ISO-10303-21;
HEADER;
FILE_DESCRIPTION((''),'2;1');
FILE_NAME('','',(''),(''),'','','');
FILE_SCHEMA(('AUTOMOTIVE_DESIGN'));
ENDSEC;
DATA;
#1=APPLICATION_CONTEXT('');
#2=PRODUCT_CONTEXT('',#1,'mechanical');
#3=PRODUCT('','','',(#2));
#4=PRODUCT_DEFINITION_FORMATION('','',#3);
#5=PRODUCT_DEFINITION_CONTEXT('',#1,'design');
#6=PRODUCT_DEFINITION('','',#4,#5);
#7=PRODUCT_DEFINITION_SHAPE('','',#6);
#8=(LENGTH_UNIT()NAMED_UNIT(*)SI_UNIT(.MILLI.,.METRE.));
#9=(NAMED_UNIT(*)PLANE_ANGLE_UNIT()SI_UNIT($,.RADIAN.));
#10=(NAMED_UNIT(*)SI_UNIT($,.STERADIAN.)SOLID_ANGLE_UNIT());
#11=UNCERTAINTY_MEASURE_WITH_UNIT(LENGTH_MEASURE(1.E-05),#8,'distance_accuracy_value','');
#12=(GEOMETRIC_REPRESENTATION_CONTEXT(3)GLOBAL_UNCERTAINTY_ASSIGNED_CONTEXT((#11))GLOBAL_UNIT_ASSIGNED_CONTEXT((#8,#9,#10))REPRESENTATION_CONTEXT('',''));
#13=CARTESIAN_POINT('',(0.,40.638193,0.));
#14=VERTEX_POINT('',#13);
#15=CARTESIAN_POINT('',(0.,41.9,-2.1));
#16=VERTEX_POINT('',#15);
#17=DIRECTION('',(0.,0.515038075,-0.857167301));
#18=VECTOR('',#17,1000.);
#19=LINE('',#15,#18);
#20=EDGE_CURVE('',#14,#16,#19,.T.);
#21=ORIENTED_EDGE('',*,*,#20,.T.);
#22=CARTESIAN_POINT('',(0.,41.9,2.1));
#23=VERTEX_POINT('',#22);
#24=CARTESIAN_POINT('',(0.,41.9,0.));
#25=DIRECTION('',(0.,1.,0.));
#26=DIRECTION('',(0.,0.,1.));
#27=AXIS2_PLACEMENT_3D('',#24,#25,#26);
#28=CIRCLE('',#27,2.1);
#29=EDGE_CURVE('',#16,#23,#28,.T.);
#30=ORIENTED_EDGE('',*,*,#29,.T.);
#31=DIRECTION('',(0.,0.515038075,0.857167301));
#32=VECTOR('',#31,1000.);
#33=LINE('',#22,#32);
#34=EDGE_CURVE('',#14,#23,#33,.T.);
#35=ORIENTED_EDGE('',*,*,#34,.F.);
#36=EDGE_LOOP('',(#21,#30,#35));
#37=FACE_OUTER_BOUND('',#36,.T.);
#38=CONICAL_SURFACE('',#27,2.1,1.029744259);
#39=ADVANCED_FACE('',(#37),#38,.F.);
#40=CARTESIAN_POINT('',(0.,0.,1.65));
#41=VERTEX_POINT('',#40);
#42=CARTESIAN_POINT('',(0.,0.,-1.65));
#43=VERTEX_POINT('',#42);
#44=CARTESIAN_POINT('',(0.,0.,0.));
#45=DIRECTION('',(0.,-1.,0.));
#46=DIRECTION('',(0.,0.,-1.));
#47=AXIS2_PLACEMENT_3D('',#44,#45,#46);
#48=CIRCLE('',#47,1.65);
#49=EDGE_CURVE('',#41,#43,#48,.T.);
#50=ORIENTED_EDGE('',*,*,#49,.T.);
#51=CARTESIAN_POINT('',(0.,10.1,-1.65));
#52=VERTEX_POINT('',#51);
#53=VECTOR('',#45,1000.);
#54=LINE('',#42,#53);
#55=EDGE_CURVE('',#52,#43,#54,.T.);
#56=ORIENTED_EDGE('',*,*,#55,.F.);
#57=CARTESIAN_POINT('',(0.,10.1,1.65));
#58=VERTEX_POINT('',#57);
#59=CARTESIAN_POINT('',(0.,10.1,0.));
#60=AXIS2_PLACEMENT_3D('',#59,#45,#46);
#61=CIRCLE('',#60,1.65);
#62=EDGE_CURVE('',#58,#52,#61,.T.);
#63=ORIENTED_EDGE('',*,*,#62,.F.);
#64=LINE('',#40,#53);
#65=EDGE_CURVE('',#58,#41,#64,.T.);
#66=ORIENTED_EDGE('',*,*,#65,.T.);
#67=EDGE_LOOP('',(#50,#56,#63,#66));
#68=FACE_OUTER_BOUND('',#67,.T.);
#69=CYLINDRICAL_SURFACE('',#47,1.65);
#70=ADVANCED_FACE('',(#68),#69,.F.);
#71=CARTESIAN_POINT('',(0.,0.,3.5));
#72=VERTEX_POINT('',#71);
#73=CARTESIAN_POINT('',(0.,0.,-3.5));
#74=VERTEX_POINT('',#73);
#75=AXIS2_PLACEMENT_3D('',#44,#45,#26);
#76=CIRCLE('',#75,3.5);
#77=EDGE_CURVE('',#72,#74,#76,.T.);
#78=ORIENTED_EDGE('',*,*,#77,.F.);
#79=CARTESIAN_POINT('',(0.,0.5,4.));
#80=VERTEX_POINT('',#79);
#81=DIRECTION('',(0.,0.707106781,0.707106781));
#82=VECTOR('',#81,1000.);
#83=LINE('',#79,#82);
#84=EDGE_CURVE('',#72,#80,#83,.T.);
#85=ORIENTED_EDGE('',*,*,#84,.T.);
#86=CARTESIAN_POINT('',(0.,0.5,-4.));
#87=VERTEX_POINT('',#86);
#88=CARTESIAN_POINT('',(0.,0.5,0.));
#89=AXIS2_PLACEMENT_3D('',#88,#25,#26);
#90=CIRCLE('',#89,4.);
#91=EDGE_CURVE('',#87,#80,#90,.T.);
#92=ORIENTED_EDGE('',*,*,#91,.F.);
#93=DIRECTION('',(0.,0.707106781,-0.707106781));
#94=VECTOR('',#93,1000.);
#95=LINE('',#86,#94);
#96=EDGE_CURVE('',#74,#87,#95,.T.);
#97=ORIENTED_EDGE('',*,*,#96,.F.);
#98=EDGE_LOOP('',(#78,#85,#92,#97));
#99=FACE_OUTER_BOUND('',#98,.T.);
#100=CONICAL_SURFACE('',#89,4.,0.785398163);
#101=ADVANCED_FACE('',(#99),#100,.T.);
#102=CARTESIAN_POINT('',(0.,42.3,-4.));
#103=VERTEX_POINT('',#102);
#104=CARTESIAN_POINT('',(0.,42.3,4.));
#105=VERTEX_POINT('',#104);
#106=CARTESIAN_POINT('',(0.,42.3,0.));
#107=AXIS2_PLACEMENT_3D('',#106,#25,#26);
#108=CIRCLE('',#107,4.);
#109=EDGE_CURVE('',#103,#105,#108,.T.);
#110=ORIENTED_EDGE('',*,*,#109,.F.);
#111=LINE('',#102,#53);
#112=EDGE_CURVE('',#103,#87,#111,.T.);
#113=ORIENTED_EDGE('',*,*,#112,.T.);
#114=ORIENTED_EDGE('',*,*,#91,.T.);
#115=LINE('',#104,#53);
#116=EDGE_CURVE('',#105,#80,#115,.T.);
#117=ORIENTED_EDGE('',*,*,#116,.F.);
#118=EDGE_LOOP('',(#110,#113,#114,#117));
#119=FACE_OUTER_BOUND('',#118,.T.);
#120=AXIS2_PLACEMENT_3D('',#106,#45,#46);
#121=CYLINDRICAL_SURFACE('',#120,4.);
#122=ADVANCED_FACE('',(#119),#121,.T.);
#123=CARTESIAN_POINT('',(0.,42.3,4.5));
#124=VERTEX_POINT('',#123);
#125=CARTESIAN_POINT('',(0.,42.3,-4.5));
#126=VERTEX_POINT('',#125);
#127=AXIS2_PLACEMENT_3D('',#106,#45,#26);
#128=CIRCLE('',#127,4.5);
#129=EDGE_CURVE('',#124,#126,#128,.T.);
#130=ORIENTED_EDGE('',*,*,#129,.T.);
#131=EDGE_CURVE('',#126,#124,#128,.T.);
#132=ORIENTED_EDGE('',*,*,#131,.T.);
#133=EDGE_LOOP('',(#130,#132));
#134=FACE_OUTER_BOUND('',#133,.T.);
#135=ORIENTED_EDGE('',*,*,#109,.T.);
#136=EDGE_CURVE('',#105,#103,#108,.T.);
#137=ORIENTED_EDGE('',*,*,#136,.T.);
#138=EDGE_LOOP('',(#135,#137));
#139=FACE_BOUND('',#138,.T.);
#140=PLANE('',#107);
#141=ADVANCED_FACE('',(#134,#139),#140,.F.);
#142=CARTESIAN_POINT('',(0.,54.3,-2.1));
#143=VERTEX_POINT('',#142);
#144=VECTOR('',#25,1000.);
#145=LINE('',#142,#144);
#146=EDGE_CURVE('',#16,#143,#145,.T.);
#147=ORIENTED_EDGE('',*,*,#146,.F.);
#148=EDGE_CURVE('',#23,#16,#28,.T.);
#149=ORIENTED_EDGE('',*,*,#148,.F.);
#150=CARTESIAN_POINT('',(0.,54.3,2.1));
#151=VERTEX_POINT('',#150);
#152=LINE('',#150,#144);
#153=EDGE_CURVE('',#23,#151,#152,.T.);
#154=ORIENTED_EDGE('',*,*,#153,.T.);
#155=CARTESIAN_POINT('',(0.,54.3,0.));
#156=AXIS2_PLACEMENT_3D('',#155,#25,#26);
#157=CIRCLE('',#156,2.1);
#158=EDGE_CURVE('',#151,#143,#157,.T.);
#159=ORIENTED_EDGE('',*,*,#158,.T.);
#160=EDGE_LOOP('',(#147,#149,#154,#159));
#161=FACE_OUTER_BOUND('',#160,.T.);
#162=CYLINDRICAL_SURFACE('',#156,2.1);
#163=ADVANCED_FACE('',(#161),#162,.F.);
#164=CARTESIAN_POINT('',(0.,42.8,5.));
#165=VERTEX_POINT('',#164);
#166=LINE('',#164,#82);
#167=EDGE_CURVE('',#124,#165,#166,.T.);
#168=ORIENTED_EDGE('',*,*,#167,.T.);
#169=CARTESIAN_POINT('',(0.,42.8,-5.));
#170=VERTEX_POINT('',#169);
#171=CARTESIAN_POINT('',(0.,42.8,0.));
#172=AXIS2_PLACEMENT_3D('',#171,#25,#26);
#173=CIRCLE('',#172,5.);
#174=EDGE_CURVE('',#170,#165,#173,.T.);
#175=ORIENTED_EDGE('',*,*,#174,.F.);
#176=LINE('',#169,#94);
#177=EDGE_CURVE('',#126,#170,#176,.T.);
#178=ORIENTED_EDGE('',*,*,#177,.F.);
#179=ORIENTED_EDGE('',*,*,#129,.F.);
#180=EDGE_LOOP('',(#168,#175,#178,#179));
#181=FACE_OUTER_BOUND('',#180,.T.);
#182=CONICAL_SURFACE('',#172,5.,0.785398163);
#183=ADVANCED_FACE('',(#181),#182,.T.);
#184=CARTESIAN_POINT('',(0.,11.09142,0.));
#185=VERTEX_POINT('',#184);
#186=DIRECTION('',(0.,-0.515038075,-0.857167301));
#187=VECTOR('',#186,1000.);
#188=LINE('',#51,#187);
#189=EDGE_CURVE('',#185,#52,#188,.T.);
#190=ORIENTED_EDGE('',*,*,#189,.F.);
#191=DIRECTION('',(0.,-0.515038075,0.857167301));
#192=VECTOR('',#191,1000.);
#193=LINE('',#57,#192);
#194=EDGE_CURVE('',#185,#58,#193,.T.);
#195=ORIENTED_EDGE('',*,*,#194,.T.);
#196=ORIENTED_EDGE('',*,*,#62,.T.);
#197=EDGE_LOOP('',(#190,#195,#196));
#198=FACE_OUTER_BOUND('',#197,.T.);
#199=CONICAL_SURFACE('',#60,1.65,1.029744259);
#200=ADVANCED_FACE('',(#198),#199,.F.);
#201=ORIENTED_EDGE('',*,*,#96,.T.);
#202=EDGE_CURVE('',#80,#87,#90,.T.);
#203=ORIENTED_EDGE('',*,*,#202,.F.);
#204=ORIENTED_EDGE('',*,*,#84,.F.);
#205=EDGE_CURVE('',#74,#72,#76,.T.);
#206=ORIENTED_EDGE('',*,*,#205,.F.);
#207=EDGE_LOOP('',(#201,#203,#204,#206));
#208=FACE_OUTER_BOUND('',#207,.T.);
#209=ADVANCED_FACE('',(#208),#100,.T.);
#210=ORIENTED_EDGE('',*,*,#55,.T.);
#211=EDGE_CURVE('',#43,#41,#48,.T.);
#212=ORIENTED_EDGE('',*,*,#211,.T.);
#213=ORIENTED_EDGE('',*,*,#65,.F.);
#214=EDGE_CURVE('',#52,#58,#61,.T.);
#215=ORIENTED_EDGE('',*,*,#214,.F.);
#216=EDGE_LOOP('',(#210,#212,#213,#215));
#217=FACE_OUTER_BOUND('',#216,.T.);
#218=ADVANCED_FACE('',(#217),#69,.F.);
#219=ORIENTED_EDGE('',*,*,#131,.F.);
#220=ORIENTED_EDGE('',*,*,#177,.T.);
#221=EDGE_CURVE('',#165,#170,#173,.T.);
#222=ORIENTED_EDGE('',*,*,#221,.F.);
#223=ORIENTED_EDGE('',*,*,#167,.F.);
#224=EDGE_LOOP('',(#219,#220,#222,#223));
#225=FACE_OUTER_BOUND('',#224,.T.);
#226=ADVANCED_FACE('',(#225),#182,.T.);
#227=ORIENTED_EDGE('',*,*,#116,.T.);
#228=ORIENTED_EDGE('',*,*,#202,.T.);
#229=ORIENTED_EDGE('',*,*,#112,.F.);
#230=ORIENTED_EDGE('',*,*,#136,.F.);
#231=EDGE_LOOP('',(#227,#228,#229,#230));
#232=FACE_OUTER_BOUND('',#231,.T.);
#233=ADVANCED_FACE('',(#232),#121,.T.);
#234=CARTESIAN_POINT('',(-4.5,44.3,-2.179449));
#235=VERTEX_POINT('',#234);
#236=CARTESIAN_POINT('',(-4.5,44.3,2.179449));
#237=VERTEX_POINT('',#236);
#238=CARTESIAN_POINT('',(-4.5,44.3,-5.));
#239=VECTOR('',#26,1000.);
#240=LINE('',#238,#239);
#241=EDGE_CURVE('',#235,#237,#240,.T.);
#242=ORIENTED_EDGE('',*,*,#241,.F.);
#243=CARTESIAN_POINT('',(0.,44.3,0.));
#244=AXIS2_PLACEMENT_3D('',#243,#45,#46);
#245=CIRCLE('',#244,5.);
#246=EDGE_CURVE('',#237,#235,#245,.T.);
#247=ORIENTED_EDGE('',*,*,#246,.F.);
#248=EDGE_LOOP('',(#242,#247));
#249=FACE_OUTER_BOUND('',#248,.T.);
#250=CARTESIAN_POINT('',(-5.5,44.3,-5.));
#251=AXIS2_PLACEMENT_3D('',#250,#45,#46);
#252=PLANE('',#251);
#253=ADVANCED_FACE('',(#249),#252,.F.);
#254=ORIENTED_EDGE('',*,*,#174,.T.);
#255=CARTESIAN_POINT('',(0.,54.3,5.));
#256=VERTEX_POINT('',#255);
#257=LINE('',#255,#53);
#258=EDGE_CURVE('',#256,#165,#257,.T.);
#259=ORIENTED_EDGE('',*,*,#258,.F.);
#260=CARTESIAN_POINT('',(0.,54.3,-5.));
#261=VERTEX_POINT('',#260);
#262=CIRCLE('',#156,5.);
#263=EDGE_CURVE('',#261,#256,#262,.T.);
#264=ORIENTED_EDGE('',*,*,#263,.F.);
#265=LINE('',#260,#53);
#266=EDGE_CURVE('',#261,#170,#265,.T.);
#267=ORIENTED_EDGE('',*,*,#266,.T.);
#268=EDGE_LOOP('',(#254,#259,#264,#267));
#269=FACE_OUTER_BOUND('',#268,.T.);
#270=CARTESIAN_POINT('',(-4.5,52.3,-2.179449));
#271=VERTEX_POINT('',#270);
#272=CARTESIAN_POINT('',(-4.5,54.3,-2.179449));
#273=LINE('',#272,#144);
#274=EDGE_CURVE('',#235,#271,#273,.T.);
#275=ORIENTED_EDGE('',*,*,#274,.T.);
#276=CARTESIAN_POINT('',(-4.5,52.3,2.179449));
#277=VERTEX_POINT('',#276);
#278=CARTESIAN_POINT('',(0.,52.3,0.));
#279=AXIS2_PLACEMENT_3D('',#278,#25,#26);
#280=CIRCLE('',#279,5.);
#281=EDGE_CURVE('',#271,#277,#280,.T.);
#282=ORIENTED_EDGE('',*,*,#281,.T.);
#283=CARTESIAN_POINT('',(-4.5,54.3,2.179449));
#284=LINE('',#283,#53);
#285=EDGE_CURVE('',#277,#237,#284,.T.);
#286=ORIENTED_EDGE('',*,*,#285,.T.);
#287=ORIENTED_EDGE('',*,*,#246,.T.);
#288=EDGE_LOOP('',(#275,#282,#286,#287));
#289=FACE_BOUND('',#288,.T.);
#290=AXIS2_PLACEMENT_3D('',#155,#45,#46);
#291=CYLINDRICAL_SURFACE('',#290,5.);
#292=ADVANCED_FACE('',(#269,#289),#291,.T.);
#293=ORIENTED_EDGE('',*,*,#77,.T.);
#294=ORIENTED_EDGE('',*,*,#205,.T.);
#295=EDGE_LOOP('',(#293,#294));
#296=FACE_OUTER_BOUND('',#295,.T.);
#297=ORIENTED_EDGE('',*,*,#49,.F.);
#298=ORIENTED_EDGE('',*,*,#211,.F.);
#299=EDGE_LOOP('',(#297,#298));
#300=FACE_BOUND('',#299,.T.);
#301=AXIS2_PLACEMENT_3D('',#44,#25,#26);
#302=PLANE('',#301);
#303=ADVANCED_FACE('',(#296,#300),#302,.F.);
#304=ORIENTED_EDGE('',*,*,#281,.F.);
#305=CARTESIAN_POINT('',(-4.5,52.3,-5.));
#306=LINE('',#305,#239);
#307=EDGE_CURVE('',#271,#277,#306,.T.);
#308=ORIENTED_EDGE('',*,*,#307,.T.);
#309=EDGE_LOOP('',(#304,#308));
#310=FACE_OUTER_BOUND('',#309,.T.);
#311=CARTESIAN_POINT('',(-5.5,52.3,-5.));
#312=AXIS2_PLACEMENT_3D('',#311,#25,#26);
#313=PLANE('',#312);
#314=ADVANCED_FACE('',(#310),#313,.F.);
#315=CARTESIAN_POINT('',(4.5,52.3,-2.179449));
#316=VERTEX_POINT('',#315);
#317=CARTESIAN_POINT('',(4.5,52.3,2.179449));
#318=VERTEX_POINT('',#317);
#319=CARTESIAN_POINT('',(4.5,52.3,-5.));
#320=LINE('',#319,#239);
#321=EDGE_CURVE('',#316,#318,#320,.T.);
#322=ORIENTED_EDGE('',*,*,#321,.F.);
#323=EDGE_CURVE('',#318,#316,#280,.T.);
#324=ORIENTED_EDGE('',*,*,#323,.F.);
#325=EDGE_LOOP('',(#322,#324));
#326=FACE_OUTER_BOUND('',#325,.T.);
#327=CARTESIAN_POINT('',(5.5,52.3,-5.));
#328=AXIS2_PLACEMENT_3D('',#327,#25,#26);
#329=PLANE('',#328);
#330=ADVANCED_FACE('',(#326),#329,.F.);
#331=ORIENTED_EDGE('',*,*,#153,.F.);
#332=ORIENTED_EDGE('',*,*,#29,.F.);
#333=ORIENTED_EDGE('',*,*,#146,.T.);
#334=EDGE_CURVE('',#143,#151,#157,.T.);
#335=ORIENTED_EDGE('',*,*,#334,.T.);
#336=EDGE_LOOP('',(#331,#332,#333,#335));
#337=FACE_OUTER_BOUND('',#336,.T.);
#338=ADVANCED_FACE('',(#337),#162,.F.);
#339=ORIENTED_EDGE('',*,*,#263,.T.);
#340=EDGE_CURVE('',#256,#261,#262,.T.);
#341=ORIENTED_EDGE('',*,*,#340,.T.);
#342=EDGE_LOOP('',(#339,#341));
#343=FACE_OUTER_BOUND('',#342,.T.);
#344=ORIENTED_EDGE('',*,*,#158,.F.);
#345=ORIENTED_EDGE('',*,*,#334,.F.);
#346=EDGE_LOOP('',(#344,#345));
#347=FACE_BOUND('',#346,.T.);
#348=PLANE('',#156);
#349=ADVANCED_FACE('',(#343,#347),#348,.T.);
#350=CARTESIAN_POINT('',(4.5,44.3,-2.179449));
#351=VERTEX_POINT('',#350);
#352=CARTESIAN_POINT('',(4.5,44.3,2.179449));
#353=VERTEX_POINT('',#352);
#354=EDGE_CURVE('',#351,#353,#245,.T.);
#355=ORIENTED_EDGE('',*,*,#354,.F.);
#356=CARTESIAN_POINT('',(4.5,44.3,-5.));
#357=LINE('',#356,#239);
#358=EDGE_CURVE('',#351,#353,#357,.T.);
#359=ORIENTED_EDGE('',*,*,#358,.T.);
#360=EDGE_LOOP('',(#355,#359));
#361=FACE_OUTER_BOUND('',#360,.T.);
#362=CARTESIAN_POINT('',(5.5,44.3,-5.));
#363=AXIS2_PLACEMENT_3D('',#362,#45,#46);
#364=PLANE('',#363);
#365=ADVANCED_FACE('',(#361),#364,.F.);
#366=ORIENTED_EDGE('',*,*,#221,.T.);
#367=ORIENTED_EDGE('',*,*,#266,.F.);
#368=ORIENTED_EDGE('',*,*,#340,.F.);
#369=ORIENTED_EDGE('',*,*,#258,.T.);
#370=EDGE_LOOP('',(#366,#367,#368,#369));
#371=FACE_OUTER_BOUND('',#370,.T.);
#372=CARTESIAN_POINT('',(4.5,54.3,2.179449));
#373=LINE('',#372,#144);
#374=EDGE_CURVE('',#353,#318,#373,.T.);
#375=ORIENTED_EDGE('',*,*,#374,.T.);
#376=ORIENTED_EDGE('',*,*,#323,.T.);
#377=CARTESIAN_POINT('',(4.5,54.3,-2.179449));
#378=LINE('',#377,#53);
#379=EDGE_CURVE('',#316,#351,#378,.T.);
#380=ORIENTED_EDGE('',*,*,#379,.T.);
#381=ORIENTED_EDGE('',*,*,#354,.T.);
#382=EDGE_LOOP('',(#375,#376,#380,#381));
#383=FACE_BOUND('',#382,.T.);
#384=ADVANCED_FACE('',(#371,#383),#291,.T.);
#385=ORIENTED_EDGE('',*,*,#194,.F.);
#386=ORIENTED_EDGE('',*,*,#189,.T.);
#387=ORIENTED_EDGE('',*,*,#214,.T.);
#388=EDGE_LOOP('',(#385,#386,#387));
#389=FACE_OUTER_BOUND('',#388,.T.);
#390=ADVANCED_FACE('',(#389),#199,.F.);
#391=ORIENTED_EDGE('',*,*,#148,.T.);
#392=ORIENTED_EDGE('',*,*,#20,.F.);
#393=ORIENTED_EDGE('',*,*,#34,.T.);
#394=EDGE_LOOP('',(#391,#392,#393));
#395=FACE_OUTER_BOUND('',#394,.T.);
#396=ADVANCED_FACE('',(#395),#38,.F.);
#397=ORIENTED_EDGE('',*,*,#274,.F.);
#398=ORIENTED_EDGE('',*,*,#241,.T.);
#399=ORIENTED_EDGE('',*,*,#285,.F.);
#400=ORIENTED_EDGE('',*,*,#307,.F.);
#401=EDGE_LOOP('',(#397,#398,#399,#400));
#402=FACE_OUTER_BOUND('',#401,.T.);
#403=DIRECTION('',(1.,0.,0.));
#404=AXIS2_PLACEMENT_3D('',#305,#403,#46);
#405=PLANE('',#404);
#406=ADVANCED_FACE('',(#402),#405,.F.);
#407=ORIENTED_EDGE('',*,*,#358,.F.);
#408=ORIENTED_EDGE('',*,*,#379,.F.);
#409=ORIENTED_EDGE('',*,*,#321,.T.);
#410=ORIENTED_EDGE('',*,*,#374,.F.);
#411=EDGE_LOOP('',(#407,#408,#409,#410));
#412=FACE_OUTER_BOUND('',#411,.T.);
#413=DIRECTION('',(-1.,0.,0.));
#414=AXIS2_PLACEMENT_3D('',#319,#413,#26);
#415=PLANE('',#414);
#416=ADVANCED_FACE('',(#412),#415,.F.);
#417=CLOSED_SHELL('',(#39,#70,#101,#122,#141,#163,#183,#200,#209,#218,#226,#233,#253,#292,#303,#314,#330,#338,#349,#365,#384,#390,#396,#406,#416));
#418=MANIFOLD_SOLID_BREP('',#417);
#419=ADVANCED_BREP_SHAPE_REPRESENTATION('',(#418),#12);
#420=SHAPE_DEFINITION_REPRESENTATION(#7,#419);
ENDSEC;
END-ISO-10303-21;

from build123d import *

# Parameters (mm, degrees)
SKETCH1_R             = 4
BOSS_EXTRUDE1_DEPTH   = 42.3
SKETCH2_R             = 5
BOSS_EXTRUDE2_DEPTH   = 12
M5_TAPPED_HOLE1_D     = 4.2
M5_TAPPED_HOLE1_DEPTH = 12.4
M5_TAPPED_HOLE1_TIP   = 1.2618073
M4_TAPPED_HOLE1_D     = 3.3
M4_TAPPED_HOLE1_DEPTH = 10.1
M4_TAPPED_HOLE1_TIP   = 0.991420021
SKETCH5_W             = 1
SKETCH5_H             = 8
CUT_EXTRUDE1_DEPTH    = 5
CHAMFER1_SIZE         = 0.5


with BuildPart() as part:
    # Sketch1 → Boss-Extrude1 (new body)
    with BuildSketch(Plane(origin=(0, 0, 0), x_dir=(1, 0, 0), z_dir=(0, 1, 0))):
        with Locations(Location((0, 0, 0), (0, 0, 270))):
            Circle(SKETCH1_R)
    extrude(amount=BOSS_EXTRUDE1_DEPTH)

    # Sketch2 → Boss-Extrude2 (add)
    with BuildSketch(Plane(origin=(0, 42.3, 0), x_dir=(1, 0, 0), z_dir=(0, 1, 0))):
        with Locations(Location((0, 0, 0), (0, 0, 270))):
            Circle(SKETCH2_R)
    extrude(amount=BOSS_EXTRUDE2_DEPTH)

    # M5 Tapped Hole1
    with Locations(Plane.ZX.offset(54.3)):
        with Locations((0, 0)):
            Hole(M5_TAPPED_HOLE1_D / 2, depth=M5_TAPPED_HOLE1_DEPTH)
            with Locations((0, 0, -(M5_TAPPED_HOLE1_DEPTH + M5_TAPPED_HOLE1_TIP / 2))):  # 118° drill point
                Cone(0, M5_TAPPED_HOLE1_D / 2, M5_TAPPED_HOLE1_TIP, mode=Mode.SUBTRACT)

    # M4 Tapped Hole1
    with Locations(Plane(origin=(0, 0, 0), x_dir=(0, 0, -1), z_dir=(0, -1, 0))):
        with Locations((0, 0)):
            Hole(M4_TAPPED_HOLE1_D / 2, depth=M4_TAPPED_HOLE1_DEPTH)
            with Locations((0, 0, -(M4_TAPPED_HOLE1_DEPTH + M4_TAPPED_HOLE1_TIP / 2))):  # 118° drill point
                Cone(0, M4_TAPPED_HOLE1_D / 2, M4_TAPPED_HOLE1_TIP, mode=Mode.SUBTRACT)

    # Sketch5 → Cut-Extrude1 (cut, symmetric)
    with BuildSketch(Plane.XY):
        with Locations((-5, 48.3)):
            Rectangle(SKETCH5_W, SKETCH5_H)
        with Locations((5, 48.3)):
            Rectangle(SKETCH5_W, SKETCH5_H)
    extrude(amount=CUT_EXTRUDE1_DEPTH, both=True, mode=Mode.SUBTRACT)

    # Chamfer1
    chamfer1_edges = [part.edges().sort_by_distance(p)[0] for p in [
        (0, 0, -4),
        (0, 42.3, -5),
    ]]
    chamfer(chamfer1_edges, length=CHAMFER1_SIZE)


solid = part.part
